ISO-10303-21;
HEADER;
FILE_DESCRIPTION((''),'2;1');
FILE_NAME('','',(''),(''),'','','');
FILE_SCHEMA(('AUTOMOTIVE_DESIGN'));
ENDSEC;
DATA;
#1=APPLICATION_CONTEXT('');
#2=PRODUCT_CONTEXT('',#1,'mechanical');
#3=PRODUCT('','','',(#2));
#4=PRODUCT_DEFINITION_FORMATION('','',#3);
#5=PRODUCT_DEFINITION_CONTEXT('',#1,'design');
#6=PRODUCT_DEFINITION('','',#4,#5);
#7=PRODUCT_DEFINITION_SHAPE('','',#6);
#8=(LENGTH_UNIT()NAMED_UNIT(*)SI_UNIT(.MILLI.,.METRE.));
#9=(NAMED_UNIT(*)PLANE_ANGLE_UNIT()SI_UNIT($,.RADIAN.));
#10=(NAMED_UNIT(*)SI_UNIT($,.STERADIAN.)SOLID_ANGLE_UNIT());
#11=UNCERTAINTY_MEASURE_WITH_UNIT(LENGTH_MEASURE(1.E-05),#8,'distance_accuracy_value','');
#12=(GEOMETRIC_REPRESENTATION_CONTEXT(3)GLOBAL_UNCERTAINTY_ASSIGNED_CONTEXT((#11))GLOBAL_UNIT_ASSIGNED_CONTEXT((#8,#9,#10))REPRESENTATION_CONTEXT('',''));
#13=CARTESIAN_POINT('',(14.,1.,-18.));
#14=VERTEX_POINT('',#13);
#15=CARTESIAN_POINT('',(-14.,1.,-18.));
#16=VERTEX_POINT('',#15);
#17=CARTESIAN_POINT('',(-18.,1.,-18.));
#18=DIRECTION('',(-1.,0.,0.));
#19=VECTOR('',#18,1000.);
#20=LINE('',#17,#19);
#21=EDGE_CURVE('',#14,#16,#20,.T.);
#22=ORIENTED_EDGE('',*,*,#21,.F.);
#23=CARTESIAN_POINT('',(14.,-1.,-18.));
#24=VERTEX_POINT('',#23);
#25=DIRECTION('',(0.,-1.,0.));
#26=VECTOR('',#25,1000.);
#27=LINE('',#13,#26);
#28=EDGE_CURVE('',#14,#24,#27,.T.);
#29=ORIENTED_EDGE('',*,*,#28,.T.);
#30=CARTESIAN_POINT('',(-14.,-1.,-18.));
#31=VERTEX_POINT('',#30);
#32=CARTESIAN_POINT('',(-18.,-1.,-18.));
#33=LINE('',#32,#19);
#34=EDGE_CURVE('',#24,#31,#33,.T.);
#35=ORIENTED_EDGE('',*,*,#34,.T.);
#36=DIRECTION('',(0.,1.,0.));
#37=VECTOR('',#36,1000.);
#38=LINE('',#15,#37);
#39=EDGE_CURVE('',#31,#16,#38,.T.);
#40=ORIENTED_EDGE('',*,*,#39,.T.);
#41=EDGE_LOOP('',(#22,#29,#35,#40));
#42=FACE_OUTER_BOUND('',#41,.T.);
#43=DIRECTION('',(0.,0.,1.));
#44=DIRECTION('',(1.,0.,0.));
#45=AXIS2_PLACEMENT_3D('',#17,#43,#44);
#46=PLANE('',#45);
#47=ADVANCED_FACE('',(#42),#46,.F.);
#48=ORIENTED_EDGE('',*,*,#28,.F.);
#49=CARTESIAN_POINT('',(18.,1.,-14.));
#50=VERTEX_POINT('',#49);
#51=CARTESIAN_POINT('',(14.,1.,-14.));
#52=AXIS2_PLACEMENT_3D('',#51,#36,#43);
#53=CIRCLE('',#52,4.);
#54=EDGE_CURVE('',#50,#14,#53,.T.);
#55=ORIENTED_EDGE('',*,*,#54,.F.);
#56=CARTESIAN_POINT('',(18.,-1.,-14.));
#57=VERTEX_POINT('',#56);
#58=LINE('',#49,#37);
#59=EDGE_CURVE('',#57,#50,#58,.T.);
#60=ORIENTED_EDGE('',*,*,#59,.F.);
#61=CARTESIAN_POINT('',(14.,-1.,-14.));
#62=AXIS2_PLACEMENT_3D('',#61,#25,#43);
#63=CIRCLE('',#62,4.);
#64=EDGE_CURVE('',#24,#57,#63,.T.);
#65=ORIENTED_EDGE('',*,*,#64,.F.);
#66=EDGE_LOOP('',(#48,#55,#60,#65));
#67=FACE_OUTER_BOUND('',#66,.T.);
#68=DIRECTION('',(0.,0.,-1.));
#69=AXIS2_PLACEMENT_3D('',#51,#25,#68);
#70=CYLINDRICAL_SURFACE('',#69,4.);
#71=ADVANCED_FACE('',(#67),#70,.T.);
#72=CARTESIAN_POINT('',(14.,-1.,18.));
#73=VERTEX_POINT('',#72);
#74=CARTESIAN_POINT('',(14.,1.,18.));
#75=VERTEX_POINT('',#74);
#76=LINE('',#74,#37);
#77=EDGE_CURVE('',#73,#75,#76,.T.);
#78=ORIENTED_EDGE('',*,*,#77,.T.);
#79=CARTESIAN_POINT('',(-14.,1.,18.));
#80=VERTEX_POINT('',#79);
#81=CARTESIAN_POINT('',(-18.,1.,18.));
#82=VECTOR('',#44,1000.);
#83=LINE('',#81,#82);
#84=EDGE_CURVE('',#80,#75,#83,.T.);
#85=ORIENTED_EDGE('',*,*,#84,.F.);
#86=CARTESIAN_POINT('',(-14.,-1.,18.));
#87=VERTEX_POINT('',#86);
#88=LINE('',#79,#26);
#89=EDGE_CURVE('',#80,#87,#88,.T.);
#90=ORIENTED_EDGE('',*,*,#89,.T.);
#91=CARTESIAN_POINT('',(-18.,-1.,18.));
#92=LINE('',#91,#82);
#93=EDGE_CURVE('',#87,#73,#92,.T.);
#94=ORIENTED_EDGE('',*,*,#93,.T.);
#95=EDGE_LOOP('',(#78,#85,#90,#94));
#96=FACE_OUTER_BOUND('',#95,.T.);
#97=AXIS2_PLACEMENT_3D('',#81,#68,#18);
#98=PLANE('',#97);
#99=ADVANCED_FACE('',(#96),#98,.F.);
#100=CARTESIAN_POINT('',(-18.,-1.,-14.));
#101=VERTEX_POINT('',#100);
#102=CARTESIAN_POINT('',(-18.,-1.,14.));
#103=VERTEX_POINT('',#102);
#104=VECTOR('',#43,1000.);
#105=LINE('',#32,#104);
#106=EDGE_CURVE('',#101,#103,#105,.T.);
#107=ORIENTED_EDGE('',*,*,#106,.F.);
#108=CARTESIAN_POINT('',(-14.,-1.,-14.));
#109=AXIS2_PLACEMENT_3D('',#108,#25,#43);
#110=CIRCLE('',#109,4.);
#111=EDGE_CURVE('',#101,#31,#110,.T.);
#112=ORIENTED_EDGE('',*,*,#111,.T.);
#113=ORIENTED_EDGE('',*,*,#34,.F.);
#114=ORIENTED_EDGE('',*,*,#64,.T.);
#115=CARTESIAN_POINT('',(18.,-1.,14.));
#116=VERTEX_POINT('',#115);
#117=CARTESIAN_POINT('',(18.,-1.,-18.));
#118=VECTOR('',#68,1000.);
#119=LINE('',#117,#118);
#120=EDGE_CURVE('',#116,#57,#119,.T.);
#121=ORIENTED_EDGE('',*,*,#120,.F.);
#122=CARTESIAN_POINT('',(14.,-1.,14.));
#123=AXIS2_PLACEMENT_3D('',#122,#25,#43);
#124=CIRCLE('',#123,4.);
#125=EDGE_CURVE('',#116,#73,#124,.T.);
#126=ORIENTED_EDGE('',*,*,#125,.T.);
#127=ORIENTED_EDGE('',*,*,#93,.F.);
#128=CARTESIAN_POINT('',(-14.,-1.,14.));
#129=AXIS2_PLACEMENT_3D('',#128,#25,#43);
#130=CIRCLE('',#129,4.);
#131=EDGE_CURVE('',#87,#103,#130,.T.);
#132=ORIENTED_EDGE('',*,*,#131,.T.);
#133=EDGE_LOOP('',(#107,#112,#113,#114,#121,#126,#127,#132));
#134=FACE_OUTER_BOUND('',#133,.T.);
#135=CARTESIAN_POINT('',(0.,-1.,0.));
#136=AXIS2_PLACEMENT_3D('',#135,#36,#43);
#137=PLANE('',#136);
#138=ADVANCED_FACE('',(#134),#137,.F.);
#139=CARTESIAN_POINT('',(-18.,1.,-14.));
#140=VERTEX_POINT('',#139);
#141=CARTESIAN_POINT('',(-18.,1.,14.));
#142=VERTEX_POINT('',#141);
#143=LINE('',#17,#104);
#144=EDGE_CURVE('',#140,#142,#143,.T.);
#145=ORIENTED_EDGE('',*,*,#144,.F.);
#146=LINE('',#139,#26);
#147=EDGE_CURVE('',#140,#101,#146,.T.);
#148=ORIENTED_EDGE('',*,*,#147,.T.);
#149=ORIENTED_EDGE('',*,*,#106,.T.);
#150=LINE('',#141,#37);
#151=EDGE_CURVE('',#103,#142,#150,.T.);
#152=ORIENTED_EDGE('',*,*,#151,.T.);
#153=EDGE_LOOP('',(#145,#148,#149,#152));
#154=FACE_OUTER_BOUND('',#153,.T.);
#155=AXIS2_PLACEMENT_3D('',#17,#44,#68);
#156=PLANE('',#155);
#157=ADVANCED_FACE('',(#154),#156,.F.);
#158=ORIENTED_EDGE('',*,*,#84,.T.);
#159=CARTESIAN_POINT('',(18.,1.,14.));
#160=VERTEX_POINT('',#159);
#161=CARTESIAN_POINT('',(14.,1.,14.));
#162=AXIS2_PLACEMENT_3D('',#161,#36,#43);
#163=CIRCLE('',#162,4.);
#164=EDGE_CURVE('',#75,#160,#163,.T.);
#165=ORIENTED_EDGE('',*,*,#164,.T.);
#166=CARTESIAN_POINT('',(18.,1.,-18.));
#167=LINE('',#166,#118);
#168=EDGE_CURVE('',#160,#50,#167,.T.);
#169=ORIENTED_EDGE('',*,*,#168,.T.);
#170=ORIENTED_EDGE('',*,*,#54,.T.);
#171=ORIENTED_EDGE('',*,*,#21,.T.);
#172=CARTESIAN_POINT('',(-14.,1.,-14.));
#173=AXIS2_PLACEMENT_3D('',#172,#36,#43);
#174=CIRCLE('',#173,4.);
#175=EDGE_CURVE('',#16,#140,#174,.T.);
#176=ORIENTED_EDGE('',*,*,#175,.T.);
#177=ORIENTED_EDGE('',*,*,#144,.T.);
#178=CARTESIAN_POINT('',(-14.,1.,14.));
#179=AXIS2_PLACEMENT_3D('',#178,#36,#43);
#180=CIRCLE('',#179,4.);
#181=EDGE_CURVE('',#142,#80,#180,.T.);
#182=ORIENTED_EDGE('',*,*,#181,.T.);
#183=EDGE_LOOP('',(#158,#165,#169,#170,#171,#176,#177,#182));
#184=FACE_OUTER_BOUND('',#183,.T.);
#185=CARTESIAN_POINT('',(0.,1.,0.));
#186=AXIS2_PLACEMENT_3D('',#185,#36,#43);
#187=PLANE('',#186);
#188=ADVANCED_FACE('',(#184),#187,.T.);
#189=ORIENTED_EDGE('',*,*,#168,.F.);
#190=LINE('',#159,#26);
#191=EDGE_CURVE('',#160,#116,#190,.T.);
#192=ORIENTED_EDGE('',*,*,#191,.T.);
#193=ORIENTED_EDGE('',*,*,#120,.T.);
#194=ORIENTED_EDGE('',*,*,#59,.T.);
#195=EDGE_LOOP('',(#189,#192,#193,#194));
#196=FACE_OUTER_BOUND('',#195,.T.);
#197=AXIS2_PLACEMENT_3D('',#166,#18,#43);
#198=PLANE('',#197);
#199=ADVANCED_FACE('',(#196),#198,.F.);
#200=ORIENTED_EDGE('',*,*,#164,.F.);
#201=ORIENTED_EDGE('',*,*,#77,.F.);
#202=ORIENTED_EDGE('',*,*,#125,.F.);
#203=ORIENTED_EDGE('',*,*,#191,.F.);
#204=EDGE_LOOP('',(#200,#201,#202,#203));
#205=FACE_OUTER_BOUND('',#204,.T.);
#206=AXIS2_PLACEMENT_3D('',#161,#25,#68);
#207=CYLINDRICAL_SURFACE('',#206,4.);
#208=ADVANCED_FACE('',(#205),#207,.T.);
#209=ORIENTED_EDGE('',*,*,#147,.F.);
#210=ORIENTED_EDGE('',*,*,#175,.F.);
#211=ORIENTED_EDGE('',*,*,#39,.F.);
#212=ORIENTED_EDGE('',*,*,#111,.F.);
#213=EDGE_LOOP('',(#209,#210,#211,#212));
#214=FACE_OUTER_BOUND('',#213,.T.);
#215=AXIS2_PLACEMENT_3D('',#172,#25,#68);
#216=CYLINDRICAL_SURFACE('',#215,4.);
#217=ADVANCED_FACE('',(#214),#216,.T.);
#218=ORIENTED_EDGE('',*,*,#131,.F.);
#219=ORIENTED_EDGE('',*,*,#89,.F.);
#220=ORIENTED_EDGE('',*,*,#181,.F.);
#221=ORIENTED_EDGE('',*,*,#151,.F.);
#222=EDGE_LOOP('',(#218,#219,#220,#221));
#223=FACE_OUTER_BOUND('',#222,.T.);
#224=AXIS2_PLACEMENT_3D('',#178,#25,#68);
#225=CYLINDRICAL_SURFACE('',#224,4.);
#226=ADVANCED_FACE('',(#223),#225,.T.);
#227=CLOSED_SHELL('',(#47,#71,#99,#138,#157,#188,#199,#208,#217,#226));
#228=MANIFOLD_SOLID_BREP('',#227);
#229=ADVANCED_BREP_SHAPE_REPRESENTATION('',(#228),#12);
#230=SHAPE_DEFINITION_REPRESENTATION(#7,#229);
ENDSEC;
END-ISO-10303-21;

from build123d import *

# Parameters (mm, degrees)
SKETCH1_W           = 36
SKETCH1_H           = 36
BOSS_EXTRUDE1_DEPTH = 1
FILLET1_R           = 4


with BuildPart() as part:
    # Sketch1 → Boss-Extrude1 (new, symmetric)
    with BuildSketch(Plane(origin=(0, 0, 0), x_dir=(1, 0, 0), z_dir=(0, 1, 0))):
        Rectangle(SKETCH1_W, SKETCH1_H)
    extrude(amount=BOSS_EXTRUDE1_DEPTH, both=True)

    # Fillet1
    fillet1_edges = [part.edges().sort_by_distance(p)[0] for p in [
        (18, 0, 18),
        (-18, 0, 18),
        (-18, 0, -18),
        (18, 0, -18),
    ]]
    fillet(fillet1_edges, radius=FILLET1_R)


solid = part.part
